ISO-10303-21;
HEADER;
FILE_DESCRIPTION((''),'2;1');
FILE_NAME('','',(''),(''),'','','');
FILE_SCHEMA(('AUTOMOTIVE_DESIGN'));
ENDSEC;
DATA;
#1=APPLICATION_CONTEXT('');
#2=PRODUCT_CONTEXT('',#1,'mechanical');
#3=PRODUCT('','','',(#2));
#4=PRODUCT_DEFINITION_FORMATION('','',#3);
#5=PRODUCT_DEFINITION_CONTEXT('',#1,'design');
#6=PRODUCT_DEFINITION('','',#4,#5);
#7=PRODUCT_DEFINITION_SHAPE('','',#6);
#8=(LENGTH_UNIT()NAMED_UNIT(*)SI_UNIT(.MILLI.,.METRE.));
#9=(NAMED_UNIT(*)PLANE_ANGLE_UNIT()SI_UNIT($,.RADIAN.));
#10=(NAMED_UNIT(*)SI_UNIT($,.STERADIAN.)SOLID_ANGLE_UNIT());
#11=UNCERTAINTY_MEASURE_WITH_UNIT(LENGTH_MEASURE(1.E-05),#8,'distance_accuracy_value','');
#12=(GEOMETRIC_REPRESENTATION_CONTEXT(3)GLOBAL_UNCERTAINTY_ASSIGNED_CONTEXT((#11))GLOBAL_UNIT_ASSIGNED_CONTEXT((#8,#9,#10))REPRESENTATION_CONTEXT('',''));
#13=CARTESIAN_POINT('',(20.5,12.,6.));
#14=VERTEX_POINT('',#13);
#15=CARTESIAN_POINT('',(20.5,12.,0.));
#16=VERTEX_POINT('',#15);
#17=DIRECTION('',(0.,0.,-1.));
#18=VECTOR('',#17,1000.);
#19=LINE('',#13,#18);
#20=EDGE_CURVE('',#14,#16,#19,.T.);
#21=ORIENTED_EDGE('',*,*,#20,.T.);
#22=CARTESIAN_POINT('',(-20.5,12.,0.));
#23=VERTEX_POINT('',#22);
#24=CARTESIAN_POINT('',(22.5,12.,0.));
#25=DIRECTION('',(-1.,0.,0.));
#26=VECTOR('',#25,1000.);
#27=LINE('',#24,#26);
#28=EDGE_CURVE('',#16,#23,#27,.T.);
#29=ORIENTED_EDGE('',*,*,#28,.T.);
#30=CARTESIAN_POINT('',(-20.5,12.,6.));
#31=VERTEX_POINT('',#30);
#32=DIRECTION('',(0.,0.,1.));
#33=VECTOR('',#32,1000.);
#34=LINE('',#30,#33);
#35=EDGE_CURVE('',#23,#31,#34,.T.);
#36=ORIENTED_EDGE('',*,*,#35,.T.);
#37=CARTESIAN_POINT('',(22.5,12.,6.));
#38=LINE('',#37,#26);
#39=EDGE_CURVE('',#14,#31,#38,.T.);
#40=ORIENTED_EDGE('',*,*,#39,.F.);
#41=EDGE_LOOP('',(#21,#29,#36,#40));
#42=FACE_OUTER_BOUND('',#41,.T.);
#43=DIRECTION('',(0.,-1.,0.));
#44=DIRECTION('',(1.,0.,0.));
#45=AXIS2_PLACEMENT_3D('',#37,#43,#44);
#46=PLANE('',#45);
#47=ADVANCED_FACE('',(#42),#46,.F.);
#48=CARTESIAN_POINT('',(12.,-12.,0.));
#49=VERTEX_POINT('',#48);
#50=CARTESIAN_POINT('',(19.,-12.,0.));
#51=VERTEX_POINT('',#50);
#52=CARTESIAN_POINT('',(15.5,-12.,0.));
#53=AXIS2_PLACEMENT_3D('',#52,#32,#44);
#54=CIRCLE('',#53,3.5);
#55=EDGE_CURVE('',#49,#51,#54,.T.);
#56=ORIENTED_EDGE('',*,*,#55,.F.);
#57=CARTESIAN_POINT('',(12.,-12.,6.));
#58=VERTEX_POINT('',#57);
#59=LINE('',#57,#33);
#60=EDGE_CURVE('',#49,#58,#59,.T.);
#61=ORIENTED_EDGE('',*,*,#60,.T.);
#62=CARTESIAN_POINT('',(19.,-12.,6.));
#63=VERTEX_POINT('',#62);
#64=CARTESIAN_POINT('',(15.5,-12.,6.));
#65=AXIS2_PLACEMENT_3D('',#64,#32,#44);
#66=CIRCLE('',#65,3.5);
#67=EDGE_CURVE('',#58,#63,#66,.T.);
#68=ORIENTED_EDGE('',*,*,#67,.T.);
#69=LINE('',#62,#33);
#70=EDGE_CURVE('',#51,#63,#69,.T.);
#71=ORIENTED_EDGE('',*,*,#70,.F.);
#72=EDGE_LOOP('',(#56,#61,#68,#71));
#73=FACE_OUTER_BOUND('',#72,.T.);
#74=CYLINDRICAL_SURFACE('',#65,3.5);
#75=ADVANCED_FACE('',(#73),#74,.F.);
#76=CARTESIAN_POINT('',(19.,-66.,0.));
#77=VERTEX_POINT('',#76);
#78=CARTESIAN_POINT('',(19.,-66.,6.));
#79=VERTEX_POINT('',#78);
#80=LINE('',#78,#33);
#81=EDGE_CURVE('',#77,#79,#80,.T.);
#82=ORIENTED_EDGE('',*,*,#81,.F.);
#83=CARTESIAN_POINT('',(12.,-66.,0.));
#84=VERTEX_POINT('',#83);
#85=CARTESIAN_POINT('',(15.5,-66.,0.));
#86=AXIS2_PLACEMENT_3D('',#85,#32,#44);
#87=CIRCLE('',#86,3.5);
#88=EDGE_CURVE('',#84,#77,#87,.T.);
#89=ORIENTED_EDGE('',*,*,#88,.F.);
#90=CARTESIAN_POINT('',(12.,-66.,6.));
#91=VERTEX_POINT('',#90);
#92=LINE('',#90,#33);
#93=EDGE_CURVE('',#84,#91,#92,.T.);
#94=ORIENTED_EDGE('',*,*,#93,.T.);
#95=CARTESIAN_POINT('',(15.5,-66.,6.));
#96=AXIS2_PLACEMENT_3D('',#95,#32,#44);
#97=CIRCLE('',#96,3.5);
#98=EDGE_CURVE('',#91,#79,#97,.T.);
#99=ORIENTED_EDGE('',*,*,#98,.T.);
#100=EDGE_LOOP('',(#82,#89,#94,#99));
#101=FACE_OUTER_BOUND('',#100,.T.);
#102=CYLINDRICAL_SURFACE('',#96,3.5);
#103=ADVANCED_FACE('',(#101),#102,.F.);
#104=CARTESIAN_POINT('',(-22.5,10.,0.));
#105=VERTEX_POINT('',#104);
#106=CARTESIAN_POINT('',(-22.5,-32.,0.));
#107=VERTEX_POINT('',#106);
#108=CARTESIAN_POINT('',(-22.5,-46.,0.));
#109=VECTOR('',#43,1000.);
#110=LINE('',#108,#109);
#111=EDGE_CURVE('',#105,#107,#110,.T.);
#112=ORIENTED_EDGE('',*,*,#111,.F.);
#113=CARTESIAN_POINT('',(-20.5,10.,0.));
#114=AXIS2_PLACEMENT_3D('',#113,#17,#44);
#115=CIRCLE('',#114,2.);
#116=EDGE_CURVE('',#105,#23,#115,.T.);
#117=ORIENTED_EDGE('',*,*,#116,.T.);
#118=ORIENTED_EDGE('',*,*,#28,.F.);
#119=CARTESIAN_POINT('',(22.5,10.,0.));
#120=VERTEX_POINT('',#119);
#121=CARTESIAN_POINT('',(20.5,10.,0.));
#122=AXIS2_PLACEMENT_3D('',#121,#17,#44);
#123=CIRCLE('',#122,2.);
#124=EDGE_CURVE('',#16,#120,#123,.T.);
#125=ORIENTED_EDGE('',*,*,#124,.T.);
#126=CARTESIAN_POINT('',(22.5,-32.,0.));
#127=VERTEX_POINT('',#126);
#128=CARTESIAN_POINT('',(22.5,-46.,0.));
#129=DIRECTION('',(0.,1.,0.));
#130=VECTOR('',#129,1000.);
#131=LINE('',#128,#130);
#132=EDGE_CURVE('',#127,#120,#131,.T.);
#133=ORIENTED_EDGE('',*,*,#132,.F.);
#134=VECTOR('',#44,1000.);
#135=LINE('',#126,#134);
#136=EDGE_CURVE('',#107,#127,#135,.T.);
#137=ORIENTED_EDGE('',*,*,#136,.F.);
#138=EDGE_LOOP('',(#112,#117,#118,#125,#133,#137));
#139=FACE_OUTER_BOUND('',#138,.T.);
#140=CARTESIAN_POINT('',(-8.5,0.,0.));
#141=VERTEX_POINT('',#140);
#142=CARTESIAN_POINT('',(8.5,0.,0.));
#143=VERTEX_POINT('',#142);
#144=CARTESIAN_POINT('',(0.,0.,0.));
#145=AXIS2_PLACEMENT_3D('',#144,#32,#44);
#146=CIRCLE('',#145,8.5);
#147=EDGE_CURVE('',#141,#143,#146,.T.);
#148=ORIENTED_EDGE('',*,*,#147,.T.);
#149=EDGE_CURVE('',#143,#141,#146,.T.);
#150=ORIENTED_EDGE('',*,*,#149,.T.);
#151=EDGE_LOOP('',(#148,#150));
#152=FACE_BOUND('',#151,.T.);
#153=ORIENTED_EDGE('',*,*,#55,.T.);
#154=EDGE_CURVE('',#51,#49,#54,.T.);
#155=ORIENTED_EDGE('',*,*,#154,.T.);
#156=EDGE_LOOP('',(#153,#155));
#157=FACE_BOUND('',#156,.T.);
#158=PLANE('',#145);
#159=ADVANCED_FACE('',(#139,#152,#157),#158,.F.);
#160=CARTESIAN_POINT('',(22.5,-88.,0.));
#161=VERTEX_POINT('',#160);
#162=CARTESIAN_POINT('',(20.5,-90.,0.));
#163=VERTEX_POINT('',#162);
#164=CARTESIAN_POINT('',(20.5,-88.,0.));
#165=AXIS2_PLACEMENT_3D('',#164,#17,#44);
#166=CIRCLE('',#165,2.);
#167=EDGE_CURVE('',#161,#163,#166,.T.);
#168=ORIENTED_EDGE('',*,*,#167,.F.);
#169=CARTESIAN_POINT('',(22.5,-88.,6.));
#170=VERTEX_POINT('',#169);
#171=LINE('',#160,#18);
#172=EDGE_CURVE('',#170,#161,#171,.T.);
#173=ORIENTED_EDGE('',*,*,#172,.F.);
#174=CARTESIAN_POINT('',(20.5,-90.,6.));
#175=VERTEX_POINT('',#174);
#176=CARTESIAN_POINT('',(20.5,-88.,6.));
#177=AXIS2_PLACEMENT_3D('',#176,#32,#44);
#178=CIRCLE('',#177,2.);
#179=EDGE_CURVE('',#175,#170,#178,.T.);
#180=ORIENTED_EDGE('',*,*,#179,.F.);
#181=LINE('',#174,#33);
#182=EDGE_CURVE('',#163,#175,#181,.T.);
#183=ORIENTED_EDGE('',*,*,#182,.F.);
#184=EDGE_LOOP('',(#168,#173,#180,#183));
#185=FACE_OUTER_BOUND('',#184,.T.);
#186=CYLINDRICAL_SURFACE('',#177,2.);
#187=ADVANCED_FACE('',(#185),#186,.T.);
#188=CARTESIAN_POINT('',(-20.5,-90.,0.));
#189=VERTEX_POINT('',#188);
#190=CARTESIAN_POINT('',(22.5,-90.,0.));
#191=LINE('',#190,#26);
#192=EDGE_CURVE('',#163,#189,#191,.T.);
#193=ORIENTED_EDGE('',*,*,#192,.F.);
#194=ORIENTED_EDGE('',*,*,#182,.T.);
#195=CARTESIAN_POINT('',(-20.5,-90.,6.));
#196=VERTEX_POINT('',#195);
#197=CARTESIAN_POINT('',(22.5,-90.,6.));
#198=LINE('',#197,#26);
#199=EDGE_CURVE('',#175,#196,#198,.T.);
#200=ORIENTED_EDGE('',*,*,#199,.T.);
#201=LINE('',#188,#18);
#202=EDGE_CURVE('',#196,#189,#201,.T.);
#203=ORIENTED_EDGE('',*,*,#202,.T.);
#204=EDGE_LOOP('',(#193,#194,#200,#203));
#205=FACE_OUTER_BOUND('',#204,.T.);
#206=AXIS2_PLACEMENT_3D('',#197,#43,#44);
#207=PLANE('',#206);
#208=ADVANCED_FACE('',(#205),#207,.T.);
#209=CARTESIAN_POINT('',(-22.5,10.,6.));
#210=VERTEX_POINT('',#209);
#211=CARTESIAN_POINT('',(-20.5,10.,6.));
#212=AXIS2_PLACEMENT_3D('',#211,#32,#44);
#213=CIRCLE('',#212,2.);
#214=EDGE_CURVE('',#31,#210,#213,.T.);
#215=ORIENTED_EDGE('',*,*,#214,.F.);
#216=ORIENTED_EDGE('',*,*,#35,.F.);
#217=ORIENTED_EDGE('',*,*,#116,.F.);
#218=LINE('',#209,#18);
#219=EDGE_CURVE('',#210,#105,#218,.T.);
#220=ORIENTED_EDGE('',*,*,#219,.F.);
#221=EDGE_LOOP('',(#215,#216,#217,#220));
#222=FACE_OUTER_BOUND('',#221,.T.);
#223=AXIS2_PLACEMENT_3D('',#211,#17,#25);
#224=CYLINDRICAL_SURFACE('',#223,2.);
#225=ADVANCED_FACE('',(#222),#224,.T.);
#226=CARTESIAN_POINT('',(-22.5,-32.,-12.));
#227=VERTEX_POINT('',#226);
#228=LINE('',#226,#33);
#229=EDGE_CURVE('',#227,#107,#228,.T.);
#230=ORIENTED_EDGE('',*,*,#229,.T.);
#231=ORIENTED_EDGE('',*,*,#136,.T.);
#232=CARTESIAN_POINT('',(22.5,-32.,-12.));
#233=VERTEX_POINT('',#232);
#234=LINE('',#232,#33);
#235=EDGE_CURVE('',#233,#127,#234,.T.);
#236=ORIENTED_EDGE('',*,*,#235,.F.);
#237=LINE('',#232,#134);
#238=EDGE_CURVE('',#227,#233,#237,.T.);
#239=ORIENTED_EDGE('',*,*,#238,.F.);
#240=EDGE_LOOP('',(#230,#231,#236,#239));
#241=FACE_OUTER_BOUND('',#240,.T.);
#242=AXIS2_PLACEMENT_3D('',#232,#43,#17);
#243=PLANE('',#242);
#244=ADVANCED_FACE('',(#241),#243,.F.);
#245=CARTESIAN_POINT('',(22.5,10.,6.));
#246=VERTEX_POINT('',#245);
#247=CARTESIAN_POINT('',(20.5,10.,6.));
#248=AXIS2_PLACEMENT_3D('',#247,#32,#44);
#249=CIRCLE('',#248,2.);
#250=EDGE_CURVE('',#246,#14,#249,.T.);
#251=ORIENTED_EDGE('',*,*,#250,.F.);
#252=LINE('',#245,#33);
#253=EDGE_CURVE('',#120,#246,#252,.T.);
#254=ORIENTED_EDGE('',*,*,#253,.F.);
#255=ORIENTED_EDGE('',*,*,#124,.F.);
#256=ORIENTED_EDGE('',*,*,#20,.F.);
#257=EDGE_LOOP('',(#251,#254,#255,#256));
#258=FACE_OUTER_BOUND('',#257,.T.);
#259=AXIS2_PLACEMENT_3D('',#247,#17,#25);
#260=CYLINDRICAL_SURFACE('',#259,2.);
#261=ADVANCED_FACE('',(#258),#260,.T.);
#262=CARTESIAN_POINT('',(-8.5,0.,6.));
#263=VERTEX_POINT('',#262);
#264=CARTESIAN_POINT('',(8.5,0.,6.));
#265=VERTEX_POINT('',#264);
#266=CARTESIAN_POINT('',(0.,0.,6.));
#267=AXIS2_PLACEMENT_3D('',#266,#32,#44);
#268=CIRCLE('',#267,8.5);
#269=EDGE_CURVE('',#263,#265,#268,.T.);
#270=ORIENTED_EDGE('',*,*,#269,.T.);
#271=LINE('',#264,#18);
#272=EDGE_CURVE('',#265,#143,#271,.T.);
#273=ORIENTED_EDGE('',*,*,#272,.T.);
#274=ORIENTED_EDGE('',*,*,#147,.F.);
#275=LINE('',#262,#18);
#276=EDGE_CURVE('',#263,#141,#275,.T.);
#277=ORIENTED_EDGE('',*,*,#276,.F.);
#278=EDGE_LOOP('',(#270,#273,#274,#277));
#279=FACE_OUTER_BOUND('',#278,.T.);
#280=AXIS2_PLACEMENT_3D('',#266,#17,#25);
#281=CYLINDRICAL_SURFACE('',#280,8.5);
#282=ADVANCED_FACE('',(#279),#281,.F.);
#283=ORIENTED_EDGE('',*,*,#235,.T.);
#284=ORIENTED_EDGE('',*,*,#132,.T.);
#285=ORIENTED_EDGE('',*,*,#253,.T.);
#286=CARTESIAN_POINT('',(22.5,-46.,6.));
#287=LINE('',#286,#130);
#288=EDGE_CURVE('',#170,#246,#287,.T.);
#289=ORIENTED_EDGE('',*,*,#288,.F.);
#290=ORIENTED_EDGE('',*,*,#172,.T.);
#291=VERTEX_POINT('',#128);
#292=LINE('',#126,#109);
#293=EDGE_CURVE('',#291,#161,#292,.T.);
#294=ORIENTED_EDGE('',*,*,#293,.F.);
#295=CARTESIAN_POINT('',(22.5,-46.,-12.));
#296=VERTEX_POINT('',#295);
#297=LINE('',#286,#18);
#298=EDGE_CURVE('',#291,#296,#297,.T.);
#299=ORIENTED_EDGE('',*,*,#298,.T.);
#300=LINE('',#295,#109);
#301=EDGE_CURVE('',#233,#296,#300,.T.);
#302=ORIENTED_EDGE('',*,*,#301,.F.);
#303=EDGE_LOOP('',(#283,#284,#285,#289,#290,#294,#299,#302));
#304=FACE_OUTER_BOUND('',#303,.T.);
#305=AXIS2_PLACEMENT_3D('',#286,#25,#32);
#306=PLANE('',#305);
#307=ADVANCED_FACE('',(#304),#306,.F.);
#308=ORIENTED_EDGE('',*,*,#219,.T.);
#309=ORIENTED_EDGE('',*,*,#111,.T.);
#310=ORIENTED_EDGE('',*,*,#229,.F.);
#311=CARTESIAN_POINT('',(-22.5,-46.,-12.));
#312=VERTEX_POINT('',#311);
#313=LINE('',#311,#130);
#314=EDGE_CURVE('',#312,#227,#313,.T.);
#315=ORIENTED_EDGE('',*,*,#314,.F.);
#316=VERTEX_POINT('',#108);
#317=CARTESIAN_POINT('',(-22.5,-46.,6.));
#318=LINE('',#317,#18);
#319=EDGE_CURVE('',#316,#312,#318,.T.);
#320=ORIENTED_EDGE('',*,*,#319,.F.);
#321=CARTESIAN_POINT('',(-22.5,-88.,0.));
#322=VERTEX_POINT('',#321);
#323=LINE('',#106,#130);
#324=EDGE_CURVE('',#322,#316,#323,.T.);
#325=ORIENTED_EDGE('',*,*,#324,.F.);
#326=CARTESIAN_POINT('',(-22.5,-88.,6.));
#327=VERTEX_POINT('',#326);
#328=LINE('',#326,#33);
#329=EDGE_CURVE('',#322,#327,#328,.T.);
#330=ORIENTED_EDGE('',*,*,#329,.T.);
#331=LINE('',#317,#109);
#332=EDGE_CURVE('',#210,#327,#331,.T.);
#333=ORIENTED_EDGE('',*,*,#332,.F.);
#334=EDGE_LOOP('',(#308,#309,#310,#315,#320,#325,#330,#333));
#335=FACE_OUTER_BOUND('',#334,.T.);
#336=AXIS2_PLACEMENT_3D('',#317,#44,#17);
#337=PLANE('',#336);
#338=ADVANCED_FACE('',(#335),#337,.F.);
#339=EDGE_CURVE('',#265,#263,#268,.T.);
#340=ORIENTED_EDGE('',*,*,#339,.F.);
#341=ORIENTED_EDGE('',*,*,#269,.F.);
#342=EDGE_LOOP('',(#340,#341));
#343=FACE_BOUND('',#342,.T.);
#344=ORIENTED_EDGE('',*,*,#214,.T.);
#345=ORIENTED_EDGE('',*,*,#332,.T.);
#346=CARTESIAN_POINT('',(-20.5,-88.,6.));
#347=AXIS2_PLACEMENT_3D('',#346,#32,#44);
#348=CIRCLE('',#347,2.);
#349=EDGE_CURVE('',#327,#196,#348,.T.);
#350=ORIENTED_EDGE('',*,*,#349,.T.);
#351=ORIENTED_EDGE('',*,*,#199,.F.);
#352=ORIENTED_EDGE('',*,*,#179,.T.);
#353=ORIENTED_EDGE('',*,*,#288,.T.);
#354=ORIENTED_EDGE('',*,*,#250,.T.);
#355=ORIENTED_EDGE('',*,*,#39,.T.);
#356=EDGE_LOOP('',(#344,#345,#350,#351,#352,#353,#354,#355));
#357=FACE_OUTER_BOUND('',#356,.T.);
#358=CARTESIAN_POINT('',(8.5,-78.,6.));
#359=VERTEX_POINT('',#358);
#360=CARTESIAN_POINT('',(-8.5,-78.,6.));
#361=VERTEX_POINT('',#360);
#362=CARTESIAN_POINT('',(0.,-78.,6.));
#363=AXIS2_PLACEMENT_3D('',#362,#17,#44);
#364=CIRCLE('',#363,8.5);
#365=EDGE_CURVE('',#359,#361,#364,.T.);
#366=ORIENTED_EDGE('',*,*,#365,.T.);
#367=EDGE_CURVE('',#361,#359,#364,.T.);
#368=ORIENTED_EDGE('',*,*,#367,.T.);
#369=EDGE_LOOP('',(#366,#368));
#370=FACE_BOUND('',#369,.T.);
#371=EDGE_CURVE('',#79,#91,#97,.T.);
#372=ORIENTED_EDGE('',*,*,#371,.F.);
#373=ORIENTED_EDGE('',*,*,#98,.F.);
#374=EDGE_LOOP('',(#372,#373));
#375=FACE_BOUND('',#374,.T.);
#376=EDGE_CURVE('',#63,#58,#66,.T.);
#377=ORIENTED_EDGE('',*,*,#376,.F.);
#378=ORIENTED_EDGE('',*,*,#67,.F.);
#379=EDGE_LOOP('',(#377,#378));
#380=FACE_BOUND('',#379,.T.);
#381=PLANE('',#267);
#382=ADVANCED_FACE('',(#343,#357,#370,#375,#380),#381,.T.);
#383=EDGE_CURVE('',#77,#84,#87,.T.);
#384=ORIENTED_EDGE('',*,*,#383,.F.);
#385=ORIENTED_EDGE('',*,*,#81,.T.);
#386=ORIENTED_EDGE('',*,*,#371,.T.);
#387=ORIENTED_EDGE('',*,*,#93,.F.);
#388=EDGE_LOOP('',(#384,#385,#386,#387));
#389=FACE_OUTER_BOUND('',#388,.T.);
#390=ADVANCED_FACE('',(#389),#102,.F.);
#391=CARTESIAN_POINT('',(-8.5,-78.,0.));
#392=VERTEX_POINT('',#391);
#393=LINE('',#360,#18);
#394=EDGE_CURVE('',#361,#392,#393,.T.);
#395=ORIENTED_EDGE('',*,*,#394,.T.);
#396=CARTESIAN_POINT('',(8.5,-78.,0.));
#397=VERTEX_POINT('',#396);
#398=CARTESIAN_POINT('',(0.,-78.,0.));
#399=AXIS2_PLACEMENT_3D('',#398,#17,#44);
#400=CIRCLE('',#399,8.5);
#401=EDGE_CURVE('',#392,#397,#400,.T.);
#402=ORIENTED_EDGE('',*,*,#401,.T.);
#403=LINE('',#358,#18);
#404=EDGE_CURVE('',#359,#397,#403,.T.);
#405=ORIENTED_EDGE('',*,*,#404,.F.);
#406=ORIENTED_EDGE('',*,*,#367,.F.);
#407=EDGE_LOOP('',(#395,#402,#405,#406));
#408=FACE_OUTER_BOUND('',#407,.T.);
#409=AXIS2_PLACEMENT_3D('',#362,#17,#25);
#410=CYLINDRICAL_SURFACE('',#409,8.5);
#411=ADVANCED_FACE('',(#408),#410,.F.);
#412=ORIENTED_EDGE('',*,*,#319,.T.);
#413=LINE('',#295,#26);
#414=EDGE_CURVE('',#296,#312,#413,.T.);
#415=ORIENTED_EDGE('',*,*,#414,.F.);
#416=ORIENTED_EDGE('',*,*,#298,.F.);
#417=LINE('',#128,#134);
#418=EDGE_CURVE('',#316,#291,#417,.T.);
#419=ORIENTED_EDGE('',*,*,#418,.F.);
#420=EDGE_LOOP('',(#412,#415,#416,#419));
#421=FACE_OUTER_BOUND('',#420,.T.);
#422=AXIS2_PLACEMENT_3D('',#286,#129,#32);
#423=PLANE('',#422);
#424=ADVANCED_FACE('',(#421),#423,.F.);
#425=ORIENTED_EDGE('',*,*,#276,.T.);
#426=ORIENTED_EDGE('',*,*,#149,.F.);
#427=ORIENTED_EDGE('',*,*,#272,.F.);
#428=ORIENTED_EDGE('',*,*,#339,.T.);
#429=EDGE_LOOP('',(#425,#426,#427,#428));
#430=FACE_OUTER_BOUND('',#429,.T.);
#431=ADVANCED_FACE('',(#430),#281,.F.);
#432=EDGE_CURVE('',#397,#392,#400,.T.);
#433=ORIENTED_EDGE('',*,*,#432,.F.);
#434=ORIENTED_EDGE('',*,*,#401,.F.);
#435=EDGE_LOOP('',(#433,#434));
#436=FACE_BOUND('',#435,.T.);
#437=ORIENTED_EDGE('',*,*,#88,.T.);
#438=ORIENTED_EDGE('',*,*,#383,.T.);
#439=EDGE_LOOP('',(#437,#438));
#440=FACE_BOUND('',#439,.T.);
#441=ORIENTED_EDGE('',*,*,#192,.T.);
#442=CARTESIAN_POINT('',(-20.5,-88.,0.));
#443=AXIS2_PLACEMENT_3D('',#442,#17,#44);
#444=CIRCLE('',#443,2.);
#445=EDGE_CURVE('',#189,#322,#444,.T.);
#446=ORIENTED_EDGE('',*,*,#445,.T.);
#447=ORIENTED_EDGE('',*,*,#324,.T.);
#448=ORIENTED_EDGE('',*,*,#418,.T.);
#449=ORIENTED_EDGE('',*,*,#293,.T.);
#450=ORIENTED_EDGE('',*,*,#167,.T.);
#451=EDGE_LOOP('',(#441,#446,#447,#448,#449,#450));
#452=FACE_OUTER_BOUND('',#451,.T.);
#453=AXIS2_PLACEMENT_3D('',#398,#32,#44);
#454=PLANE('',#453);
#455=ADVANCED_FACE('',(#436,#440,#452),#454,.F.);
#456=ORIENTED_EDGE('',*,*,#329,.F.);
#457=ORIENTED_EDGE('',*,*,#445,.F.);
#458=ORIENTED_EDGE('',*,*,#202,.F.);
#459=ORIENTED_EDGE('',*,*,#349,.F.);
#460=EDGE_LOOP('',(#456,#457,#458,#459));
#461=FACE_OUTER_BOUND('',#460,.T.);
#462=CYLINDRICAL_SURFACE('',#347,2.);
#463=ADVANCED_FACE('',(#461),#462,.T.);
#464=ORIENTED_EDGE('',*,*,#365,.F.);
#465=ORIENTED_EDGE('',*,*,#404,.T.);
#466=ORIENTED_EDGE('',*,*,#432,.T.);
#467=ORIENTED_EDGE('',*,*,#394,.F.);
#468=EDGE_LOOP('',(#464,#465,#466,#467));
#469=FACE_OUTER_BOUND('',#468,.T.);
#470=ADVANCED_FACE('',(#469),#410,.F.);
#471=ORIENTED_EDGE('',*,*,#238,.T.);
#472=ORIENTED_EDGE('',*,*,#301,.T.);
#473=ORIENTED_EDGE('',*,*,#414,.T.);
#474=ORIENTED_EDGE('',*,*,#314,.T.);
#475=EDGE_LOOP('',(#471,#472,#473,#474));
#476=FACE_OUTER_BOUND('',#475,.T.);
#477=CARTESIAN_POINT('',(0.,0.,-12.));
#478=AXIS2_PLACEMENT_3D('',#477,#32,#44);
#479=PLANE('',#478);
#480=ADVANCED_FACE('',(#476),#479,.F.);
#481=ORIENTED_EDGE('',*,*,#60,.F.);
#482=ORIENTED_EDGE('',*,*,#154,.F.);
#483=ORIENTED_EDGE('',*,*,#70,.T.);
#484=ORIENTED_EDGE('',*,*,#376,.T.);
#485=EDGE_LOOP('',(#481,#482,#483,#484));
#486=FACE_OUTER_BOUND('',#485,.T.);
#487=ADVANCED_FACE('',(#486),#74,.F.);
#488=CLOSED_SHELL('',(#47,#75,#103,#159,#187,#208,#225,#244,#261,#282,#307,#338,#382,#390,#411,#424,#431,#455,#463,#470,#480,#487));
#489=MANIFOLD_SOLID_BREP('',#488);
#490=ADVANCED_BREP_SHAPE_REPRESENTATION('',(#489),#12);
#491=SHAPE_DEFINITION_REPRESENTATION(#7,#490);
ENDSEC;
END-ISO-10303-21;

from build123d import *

# Parameters (mm, degrees)
SKETCH_1_W      = 45
SKETCH_1_H      = 58
SKETCH_1_R      = 8.5
EXTRUDE_1_DEPTH = 6
SKETCH_2_W      = 45
SKETCH_2_H      = 14
EXTRUDE_2_DEPTH = 12
M8X1_0_1_D      = 7
FILLET_1_R      = 2


with BuildPart() as part:
    # 草图1 → 凸台-拉伸1 (new body)
    with BuildSketch(Plane.XY):
        with Locations((0, -17)):
            Rectangle(SKETCH_1_W, SKETCH_1_H)
        Circle(SKETCH_1_R, mode=Mode.SUBTRACT)
    extrude_1 = extrude(amount=EXTRUDE_1_DEPTH)

    # 草图2 → 凸台-拉伸2 (add)
    with BuildSketch(Plane(origin=(0, 0, 0), x_dir=(-1, 0, 0), z_dir=(0, 0, -1))):
        with Locations((0, -39)):
            Rectangle(SKETCH_2_W, SKETCH_2_H)
    extrude(amount=EXTRUDE_2_DEPTH)

    # M8x1.0 螺纹孔1 (through all)
    with Locations(Plane(origin=(15.5, -12, 6), x_dir=(1, 0, 0), z_dir=(0, 0, 1))):
        with Locations((0, 0)):
            m8x1_0_1 = Hole(M8X1_0_1_D / 2)

    # 镜向1: 凸台-拉伸1, M8x1.0 螺纹孔1 across plane
    add(extrude_1.mirror(Plane(origin=(0, -39, 0), x_dir=(0, 0, 1), z_dir=(0, -1, 0))))
    add(m8x1_0_1.mirror(Plane(origin=(0, -39, 0), x_dir=(0, 0, 1), z_dir=(0, -1, 0))), mode=Mode.SUBTRACT)

    # 圆角1
    fillet_1_edges = [part.edges().sort_by_distance(p)[0] for p in [
        (22.5, -90, 3),
        (-22.5, -90, 3),
        (-22.5, 12, 3),
        (22.5, 12, 3),
    ]]
    fillet(fillet_1_edges, radius=FILLET_1_R)


solid = part.part
